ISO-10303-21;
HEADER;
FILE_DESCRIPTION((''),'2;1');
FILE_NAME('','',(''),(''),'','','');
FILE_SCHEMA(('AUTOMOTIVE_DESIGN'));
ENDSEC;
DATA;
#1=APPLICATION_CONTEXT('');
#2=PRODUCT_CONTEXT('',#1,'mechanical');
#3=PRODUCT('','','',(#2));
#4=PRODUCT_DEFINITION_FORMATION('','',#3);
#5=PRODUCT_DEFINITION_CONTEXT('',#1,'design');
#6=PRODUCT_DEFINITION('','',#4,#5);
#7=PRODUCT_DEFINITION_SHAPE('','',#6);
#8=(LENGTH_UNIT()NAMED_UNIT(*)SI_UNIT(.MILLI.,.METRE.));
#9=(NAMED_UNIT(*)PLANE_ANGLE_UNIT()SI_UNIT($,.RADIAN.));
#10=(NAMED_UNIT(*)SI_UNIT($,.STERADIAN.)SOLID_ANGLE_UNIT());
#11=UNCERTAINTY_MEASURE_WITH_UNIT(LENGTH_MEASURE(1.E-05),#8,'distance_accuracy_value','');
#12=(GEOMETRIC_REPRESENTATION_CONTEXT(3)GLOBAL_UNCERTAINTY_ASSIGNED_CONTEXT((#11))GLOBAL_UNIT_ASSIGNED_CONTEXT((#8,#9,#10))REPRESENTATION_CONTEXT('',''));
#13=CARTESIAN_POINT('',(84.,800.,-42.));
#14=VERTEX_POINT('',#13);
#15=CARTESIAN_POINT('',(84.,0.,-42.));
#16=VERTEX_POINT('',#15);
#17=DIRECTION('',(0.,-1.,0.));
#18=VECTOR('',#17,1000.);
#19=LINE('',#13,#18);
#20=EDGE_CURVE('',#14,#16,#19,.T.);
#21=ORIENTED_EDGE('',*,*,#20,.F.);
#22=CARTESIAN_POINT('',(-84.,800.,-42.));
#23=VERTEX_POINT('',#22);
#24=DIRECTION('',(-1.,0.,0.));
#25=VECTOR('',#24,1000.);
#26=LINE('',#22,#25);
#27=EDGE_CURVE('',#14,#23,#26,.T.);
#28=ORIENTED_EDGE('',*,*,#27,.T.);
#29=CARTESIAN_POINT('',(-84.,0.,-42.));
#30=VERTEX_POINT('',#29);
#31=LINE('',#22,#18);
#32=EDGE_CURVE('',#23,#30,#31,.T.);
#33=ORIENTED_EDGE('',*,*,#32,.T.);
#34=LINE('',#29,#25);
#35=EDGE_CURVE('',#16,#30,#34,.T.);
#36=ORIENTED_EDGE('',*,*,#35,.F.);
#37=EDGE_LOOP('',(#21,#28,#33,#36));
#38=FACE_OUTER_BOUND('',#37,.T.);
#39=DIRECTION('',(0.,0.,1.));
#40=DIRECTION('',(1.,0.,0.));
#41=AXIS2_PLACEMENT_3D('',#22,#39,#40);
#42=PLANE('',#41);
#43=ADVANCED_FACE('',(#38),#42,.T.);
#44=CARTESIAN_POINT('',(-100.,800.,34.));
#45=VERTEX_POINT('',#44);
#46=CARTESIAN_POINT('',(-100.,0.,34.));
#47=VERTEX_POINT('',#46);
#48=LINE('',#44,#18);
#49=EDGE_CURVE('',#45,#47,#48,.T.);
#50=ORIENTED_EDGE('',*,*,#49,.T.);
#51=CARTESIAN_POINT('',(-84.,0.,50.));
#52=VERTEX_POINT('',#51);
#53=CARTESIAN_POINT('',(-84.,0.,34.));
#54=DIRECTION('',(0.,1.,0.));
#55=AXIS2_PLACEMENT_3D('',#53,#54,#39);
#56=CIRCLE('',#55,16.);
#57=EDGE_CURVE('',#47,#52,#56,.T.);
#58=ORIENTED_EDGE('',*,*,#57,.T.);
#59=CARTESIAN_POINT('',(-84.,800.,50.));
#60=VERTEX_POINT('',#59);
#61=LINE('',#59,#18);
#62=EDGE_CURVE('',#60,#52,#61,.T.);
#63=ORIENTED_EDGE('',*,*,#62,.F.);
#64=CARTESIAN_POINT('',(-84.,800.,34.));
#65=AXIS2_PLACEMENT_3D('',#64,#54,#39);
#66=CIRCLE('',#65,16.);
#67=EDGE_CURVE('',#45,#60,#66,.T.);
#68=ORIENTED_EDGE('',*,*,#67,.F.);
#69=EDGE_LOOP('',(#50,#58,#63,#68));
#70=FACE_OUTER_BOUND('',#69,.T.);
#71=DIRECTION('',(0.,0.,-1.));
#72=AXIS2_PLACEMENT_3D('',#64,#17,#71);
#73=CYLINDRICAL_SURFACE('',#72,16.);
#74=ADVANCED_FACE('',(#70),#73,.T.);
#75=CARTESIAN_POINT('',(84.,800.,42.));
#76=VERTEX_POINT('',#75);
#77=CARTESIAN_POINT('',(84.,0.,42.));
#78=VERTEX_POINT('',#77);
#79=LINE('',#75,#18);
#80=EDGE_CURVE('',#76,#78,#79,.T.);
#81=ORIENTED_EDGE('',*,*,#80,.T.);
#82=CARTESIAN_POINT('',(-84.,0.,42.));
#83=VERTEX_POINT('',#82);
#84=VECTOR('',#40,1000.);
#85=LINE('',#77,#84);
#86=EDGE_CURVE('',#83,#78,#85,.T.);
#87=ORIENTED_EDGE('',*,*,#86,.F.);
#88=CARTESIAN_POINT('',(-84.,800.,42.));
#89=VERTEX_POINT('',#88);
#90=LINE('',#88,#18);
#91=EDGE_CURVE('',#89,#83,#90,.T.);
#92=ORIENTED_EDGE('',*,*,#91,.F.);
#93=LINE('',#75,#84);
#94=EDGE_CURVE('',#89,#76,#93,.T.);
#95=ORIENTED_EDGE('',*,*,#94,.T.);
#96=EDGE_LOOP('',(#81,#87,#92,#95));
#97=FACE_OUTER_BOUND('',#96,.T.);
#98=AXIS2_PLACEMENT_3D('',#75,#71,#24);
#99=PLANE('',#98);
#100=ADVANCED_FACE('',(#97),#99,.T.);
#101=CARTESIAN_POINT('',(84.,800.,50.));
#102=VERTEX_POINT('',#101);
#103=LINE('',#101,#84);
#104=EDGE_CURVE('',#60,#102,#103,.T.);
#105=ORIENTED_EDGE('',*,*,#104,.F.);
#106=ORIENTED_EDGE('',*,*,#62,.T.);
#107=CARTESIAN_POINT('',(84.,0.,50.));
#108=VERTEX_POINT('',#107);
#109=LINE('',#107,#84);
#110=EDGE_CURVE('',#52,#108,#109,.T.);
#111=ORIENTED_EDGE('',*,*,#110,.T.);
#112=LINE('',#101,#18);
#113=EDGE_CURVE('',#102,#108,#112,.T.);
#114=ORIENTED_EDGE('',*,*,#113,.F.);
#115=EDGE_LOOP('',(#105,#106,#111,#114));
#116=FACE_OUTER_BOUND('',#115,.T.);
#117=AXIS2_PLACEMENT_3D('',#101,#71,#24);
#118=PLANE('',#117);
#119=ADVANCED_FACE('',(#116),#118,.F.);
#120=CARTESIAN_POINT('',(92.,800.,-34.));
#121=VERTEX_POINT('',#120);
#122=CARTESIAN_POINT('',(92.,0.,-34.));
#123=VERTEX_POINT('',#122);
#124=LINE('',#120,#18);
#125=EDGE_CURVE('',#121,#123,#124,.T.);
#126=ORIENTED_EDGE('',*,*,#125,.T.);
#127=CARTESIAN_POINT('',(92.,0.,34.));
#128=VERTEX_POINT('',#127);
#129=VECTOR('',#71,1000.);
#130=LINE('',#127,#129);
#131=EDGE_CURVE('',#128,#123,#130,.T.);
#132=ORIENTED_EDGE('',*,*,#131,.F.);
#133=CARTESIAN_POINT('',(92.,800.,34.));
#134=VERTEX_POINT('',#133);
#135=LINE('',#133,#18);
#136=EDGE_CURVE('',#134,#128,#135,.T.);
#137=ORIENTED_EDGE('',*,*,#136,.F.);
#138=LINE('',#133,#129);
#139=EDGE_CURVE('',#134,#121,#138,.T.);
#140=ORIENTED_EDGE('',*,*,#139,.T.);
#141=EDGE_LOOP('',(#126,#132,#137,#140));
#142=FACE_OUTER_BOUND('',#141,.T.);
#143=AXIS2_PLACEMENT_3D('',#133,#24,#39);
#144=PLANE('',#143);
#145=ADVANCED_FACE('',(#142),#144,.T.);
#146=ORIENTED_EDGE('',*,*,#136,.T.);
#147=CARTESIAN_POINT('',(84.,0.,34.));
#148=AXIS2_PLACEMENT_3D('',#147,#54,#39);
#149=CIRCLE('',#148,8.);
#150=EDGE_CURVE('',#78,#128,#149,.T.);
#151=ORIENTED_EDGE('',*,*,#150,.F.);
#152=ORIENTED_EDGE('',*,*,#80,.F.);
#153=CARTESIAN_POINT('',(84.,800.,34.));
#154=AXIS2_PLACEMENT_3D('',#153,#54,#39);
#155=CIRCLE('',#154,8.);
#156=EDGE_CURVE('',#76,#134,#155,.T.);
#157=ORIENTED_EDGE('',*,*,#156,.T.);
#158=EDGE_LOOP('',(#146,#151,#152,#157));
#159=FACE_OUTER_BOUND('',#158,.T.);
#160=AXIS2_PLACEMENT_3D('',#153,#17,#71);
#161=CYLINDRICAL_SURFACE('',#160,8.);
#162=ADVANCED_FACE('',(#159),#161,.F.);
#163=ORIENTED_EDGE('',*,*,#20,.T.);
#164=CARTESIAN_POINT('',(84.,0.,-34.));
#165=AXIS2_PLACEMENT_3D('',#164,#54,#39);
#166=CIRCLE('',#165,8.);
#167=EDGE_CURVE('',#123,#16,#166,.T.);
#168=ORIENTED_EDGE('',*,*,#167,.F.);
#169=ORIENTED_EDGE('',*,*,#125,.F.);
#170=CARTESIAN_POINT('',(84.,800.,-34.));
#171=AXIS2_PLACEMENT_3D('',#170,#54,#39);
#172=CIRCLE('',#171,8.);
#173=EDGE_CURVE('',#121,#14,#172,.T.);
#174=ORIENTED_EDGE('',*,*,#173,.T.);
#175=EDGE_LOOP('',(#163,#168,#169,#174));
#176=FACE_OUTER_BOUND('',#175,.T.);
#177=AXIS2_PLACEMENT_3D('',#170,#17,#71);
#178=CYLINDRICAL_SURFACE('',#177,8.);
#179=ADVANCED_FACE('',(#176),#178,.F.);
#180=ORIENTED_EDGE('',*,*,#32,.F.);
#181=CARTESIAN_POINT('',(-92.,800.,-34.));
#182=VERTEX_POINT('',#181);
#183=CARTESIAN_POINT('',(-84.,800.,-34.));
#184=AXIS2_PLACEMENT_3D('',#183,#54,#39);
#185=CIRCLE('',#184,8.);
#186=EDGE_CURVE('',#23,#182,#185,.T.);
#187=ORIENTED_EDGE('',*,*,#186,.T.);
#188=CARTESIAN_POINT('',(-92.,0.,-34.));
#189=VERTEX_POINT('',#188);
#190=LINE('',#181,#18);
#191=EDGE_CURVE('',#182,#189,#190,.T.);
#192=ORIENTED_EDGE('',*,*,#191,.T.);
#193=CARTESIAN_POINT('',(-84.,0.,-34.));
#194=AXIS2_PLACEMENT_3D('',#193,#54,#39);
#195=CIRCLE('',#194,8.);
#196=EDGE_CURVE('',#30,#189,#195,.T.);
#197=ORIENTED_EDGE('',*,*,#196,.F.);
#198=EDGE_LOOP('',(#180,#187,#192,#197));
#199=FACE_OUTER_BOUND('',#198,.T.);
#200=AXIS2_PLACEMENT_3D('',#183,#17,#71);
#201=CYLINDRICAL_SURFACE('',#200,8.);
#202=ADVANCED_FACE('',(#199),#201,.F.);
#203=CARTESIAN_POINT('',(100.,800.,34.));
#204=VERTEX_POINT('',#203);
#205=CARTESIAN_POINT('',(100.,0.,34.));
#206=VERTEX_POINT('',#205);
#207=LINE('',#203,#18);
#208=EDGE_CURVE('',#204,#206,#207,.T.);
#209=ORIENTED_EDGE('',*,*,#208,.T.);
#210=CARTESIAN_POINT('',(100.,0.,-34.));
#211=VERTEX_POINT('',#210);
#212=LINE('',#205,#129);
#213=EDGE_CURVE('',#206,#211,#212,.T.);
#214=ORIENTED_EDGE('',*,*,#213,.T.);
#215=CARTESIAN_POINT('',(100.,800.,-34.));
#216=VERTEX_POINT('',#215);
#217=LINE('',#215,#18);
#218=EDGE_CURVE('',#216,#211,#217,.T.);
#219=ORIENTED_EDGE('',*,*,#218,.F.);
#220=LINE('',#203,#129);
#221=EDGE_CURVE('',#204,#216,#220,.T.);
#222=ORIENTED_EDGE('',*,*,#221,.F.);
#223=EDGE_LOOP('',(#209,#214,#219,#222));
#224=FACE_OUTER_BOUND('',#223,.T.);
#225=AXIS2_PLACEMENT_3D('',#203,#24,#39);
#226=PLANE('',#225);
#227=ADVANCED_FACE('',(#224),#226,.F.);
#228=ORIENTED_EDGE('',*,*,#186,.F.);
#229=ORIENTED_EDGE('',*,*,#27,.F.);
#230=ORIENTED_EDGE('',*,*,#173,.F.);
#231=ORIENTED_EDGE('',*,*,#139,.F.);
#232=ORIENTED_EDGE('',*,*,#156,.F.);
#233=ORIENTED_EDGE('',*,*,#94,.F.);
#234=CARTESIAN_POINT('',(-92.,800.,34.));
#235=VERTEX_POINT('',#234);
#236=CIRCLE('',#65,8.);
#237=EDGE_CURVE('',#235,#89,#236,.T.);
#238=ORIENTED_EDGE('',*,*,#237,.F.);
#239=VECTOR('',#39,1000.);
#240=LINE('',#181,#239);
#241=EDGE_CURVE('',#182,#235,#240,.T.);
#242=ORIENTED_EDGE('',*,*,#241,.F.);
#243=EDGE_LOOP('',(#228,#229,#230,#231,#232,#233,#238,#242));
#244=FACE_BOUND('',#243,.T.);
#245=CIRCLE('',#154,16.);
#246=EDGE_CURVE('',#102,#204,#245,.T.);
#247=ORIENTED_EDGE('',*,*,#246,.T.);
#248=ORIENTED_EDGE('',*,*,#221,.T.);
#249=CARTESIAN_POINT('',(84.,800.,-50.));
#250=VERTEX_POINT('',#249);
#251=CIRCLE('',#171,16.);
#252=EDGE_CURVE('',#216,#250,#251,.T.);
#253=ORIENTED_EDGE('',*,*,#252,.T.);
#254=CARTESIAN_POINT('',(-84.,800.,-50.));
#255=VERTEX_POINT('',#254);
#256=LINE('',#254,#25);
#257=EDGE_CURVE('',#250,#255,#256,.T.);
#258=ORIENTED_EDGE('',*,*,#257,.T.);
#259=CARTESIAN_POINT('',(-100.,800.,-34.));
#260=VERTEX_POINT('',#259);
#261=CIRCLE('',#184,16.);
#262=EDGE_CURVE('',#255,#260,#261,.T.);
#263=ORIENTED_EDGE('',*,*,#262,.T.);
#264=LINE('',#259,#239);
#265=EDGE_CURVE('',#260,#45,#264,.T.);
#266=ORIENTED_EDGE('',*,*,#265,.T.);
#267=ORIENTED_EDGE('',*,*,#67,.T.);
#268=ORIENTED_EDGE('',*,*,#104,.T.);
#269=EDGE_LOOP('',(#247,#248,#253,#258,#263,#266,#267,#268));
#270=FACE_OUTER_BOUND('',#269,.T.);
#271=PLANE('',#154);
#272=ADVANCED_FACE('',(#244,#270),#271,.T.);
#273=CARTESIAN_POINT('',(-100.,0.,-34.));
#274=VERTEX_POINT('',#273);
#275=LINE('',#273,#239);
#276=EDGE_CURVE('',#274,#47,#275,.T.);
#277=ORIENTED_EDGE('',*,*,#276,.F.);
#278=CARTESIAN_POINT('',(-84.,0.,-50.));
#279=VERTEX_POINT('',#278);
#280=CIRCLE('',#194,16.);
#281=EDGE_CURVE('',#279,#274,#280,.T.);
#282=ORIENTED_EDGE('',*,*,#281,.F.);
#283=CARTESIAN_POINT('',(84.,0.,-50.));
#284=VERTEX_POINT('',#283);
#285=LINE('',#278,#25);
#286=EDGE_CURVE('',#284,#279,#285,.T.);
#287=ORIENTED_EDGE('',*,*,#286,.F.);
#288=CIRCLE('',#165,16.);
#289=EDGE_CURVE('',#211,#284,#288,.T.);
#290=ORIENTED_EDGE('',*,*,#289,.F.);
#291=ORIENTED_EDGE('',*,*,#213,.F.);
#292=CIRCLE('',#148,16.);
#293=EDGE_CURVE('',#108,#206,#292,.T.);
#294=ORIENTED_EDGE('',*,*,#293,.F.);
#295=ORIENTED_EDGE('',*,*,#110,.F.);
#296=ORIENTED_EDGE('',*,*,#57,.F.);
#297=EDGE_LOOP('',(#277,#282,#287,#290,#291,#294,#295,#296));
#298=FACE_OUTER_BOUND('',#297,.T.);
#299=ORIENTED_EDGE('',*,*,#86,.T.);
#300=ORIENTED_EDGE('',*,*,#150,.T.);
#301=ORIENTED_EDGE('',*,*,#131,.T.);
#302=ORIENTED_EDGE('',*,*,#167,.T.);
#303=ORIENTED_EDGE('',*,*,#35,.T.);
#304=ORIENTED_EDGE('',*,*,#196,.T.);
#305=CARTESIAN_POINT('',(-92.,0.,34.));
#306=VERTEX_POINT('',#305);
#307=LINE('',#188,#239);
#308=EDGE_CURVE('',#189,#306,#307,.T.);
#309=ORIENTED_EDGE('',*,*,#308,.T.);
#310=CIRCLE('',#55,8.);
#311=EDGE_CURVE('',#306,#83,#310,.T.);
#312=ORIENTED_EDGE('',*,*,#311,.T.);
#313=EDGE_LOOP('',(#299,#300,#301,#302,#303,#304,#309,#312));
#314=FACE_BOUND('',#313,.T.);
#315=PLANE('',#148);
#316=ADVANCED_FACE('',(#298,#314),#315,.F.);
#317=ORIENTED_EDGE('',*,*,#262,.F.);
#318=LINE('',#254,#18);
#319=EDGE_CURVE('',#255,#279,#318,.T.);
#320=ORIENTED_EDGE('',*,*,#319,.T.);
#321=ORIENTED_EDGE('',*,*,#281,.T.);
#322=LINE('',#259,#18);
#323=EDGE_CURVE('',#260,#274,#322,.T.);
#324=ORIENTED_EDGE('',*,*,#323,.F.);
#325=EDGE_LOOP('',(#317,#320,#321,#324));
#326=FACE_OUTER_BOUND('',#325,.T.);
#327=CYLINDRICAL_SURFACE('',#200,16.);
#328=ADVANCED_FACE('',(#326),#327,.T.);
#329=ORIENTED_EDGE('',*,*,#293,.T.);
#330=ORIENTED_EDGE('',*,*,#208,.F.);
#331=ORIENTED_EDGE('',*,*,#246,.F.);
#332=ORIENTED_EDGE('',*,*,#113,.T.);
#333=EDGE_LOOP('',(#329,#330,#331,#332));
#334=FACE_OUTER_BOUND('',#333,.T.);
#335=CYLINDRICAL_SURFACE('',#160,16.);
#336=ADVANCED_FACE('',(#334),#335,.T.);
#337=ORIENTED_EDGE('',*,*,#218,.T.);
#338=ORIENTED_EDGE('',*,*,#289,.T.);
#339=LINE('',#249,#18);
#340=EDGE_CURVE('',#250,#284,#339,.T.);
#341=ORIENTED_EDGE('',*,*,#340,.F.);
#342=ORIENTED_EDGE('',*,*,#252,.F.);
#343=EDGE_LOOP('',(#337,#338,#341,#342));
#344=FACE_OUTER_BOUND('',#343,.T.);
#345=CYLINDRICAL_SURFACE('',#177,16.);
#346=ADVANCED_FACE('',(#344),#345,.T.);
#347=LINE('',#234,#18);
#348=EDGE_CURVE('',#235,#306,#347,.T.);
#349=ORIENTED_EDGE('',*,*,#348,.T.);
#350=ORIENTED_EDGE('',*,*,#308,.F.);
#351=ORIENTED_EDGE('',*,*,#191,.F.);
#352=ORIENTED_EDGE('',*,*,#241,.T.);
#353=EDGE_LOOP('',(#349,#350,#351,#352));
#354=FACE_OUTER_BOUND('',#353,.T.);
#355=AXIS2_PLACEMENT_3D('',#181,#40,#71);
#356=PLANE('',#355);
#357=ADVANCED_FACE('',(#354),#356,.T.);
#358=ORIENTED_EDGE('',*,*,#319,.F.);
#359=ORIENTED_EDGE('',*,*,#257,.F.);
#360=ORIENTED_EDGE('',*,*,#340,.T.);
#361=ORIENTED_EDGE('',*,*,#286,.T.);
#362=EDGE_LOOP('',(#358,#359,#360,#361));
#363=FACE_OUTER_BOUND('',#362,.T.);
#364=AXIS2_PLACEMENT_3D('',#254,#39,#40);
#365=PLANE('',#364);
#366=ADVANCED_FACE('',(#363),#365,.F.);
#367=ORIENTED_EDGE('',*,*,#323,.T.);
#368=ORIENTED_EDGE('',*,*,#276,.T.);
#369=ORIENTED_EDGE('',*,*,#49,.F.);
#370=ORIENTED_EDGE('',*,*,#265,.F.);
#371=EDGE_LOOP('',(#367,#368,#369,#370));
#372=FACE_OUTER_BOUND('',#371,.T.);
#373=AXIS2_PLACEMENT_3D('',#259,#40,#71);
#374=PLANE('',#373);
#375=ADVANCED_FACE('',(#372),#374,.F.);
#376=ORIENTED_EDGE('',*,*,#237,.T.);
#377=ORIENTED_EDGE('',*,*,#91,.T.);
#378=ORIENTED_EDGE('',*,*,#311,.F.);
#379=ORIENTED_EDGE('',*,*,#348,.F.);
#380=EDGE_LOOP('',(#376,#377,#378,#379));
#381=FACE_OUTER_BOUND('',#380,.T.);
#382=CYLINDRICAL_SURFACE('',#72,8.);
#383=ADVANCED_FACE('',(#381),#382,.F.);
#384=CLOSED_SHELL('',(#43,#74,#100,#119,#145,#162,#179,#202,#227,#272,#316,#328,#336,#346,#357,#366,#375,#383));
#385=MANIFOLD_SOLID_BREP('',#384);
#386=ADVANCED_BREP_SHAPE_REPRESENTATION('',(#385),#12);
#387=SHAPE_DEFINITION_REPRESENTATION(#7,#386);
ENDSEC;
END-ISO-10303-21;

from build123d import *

# Parameters (mm, degrees)
GB_T_6728_2002_RECTANGULAR_HOLLOW_SECTIO_DEPTH = 800


with BuildPart() as part:
    # Sketch12 → GB/T 6728-2002 rectangular hollow section 200X100X8(2) (new body)
    with BuildSketch(Plane.ZX):
        with BuildLine():
            Line((-34, -100), (34, -100))
            ThreePointArc((34, -100), (45.313708499, -95.313708499), (50, -84))
            Line((50, -84), (50, 84))
            ThreePointArc((50, 84), (45.313708499, 95.313708499), (34, 100))
            Line((34, 100), (-34, 100))
            ThreePointArc((-34, 100), (-45.313708499, 95.313708499), (-50, 84))
            Line((-50, 84), (-50, -84))
            ThreePointArc((-50, -84), (-45.313708499, -95.313708499), (-34, -100))
        make_face()
        with BuildLine():
            Line((-34, -92), (34, -92))
            ThreePointArc((34, -92), (39.656854249, -89.656854249), (42, -84))
            Line((42, -84), (42, 84))
            ThreePointArc((42, 84), (39.656854249, 89.656854249), (34, 92))
            Line((34, 92), (-34, 92))
            ThreePointArc((-34, 92), (-39.656854249, 89.656854249), (-42, 84))
            Line((-42, 84), (-42, -84))
            ThreePointArc((-42, -84), (-39.656854249, -89.656854249), (-34, -92))
        make_face(mode=Mode.SUBTRACT)
    extrude(amount=GB_T_6728_2002_RECTANGULAR_HOLLOW_SECTIO_DEPTH)


solid = part.part
